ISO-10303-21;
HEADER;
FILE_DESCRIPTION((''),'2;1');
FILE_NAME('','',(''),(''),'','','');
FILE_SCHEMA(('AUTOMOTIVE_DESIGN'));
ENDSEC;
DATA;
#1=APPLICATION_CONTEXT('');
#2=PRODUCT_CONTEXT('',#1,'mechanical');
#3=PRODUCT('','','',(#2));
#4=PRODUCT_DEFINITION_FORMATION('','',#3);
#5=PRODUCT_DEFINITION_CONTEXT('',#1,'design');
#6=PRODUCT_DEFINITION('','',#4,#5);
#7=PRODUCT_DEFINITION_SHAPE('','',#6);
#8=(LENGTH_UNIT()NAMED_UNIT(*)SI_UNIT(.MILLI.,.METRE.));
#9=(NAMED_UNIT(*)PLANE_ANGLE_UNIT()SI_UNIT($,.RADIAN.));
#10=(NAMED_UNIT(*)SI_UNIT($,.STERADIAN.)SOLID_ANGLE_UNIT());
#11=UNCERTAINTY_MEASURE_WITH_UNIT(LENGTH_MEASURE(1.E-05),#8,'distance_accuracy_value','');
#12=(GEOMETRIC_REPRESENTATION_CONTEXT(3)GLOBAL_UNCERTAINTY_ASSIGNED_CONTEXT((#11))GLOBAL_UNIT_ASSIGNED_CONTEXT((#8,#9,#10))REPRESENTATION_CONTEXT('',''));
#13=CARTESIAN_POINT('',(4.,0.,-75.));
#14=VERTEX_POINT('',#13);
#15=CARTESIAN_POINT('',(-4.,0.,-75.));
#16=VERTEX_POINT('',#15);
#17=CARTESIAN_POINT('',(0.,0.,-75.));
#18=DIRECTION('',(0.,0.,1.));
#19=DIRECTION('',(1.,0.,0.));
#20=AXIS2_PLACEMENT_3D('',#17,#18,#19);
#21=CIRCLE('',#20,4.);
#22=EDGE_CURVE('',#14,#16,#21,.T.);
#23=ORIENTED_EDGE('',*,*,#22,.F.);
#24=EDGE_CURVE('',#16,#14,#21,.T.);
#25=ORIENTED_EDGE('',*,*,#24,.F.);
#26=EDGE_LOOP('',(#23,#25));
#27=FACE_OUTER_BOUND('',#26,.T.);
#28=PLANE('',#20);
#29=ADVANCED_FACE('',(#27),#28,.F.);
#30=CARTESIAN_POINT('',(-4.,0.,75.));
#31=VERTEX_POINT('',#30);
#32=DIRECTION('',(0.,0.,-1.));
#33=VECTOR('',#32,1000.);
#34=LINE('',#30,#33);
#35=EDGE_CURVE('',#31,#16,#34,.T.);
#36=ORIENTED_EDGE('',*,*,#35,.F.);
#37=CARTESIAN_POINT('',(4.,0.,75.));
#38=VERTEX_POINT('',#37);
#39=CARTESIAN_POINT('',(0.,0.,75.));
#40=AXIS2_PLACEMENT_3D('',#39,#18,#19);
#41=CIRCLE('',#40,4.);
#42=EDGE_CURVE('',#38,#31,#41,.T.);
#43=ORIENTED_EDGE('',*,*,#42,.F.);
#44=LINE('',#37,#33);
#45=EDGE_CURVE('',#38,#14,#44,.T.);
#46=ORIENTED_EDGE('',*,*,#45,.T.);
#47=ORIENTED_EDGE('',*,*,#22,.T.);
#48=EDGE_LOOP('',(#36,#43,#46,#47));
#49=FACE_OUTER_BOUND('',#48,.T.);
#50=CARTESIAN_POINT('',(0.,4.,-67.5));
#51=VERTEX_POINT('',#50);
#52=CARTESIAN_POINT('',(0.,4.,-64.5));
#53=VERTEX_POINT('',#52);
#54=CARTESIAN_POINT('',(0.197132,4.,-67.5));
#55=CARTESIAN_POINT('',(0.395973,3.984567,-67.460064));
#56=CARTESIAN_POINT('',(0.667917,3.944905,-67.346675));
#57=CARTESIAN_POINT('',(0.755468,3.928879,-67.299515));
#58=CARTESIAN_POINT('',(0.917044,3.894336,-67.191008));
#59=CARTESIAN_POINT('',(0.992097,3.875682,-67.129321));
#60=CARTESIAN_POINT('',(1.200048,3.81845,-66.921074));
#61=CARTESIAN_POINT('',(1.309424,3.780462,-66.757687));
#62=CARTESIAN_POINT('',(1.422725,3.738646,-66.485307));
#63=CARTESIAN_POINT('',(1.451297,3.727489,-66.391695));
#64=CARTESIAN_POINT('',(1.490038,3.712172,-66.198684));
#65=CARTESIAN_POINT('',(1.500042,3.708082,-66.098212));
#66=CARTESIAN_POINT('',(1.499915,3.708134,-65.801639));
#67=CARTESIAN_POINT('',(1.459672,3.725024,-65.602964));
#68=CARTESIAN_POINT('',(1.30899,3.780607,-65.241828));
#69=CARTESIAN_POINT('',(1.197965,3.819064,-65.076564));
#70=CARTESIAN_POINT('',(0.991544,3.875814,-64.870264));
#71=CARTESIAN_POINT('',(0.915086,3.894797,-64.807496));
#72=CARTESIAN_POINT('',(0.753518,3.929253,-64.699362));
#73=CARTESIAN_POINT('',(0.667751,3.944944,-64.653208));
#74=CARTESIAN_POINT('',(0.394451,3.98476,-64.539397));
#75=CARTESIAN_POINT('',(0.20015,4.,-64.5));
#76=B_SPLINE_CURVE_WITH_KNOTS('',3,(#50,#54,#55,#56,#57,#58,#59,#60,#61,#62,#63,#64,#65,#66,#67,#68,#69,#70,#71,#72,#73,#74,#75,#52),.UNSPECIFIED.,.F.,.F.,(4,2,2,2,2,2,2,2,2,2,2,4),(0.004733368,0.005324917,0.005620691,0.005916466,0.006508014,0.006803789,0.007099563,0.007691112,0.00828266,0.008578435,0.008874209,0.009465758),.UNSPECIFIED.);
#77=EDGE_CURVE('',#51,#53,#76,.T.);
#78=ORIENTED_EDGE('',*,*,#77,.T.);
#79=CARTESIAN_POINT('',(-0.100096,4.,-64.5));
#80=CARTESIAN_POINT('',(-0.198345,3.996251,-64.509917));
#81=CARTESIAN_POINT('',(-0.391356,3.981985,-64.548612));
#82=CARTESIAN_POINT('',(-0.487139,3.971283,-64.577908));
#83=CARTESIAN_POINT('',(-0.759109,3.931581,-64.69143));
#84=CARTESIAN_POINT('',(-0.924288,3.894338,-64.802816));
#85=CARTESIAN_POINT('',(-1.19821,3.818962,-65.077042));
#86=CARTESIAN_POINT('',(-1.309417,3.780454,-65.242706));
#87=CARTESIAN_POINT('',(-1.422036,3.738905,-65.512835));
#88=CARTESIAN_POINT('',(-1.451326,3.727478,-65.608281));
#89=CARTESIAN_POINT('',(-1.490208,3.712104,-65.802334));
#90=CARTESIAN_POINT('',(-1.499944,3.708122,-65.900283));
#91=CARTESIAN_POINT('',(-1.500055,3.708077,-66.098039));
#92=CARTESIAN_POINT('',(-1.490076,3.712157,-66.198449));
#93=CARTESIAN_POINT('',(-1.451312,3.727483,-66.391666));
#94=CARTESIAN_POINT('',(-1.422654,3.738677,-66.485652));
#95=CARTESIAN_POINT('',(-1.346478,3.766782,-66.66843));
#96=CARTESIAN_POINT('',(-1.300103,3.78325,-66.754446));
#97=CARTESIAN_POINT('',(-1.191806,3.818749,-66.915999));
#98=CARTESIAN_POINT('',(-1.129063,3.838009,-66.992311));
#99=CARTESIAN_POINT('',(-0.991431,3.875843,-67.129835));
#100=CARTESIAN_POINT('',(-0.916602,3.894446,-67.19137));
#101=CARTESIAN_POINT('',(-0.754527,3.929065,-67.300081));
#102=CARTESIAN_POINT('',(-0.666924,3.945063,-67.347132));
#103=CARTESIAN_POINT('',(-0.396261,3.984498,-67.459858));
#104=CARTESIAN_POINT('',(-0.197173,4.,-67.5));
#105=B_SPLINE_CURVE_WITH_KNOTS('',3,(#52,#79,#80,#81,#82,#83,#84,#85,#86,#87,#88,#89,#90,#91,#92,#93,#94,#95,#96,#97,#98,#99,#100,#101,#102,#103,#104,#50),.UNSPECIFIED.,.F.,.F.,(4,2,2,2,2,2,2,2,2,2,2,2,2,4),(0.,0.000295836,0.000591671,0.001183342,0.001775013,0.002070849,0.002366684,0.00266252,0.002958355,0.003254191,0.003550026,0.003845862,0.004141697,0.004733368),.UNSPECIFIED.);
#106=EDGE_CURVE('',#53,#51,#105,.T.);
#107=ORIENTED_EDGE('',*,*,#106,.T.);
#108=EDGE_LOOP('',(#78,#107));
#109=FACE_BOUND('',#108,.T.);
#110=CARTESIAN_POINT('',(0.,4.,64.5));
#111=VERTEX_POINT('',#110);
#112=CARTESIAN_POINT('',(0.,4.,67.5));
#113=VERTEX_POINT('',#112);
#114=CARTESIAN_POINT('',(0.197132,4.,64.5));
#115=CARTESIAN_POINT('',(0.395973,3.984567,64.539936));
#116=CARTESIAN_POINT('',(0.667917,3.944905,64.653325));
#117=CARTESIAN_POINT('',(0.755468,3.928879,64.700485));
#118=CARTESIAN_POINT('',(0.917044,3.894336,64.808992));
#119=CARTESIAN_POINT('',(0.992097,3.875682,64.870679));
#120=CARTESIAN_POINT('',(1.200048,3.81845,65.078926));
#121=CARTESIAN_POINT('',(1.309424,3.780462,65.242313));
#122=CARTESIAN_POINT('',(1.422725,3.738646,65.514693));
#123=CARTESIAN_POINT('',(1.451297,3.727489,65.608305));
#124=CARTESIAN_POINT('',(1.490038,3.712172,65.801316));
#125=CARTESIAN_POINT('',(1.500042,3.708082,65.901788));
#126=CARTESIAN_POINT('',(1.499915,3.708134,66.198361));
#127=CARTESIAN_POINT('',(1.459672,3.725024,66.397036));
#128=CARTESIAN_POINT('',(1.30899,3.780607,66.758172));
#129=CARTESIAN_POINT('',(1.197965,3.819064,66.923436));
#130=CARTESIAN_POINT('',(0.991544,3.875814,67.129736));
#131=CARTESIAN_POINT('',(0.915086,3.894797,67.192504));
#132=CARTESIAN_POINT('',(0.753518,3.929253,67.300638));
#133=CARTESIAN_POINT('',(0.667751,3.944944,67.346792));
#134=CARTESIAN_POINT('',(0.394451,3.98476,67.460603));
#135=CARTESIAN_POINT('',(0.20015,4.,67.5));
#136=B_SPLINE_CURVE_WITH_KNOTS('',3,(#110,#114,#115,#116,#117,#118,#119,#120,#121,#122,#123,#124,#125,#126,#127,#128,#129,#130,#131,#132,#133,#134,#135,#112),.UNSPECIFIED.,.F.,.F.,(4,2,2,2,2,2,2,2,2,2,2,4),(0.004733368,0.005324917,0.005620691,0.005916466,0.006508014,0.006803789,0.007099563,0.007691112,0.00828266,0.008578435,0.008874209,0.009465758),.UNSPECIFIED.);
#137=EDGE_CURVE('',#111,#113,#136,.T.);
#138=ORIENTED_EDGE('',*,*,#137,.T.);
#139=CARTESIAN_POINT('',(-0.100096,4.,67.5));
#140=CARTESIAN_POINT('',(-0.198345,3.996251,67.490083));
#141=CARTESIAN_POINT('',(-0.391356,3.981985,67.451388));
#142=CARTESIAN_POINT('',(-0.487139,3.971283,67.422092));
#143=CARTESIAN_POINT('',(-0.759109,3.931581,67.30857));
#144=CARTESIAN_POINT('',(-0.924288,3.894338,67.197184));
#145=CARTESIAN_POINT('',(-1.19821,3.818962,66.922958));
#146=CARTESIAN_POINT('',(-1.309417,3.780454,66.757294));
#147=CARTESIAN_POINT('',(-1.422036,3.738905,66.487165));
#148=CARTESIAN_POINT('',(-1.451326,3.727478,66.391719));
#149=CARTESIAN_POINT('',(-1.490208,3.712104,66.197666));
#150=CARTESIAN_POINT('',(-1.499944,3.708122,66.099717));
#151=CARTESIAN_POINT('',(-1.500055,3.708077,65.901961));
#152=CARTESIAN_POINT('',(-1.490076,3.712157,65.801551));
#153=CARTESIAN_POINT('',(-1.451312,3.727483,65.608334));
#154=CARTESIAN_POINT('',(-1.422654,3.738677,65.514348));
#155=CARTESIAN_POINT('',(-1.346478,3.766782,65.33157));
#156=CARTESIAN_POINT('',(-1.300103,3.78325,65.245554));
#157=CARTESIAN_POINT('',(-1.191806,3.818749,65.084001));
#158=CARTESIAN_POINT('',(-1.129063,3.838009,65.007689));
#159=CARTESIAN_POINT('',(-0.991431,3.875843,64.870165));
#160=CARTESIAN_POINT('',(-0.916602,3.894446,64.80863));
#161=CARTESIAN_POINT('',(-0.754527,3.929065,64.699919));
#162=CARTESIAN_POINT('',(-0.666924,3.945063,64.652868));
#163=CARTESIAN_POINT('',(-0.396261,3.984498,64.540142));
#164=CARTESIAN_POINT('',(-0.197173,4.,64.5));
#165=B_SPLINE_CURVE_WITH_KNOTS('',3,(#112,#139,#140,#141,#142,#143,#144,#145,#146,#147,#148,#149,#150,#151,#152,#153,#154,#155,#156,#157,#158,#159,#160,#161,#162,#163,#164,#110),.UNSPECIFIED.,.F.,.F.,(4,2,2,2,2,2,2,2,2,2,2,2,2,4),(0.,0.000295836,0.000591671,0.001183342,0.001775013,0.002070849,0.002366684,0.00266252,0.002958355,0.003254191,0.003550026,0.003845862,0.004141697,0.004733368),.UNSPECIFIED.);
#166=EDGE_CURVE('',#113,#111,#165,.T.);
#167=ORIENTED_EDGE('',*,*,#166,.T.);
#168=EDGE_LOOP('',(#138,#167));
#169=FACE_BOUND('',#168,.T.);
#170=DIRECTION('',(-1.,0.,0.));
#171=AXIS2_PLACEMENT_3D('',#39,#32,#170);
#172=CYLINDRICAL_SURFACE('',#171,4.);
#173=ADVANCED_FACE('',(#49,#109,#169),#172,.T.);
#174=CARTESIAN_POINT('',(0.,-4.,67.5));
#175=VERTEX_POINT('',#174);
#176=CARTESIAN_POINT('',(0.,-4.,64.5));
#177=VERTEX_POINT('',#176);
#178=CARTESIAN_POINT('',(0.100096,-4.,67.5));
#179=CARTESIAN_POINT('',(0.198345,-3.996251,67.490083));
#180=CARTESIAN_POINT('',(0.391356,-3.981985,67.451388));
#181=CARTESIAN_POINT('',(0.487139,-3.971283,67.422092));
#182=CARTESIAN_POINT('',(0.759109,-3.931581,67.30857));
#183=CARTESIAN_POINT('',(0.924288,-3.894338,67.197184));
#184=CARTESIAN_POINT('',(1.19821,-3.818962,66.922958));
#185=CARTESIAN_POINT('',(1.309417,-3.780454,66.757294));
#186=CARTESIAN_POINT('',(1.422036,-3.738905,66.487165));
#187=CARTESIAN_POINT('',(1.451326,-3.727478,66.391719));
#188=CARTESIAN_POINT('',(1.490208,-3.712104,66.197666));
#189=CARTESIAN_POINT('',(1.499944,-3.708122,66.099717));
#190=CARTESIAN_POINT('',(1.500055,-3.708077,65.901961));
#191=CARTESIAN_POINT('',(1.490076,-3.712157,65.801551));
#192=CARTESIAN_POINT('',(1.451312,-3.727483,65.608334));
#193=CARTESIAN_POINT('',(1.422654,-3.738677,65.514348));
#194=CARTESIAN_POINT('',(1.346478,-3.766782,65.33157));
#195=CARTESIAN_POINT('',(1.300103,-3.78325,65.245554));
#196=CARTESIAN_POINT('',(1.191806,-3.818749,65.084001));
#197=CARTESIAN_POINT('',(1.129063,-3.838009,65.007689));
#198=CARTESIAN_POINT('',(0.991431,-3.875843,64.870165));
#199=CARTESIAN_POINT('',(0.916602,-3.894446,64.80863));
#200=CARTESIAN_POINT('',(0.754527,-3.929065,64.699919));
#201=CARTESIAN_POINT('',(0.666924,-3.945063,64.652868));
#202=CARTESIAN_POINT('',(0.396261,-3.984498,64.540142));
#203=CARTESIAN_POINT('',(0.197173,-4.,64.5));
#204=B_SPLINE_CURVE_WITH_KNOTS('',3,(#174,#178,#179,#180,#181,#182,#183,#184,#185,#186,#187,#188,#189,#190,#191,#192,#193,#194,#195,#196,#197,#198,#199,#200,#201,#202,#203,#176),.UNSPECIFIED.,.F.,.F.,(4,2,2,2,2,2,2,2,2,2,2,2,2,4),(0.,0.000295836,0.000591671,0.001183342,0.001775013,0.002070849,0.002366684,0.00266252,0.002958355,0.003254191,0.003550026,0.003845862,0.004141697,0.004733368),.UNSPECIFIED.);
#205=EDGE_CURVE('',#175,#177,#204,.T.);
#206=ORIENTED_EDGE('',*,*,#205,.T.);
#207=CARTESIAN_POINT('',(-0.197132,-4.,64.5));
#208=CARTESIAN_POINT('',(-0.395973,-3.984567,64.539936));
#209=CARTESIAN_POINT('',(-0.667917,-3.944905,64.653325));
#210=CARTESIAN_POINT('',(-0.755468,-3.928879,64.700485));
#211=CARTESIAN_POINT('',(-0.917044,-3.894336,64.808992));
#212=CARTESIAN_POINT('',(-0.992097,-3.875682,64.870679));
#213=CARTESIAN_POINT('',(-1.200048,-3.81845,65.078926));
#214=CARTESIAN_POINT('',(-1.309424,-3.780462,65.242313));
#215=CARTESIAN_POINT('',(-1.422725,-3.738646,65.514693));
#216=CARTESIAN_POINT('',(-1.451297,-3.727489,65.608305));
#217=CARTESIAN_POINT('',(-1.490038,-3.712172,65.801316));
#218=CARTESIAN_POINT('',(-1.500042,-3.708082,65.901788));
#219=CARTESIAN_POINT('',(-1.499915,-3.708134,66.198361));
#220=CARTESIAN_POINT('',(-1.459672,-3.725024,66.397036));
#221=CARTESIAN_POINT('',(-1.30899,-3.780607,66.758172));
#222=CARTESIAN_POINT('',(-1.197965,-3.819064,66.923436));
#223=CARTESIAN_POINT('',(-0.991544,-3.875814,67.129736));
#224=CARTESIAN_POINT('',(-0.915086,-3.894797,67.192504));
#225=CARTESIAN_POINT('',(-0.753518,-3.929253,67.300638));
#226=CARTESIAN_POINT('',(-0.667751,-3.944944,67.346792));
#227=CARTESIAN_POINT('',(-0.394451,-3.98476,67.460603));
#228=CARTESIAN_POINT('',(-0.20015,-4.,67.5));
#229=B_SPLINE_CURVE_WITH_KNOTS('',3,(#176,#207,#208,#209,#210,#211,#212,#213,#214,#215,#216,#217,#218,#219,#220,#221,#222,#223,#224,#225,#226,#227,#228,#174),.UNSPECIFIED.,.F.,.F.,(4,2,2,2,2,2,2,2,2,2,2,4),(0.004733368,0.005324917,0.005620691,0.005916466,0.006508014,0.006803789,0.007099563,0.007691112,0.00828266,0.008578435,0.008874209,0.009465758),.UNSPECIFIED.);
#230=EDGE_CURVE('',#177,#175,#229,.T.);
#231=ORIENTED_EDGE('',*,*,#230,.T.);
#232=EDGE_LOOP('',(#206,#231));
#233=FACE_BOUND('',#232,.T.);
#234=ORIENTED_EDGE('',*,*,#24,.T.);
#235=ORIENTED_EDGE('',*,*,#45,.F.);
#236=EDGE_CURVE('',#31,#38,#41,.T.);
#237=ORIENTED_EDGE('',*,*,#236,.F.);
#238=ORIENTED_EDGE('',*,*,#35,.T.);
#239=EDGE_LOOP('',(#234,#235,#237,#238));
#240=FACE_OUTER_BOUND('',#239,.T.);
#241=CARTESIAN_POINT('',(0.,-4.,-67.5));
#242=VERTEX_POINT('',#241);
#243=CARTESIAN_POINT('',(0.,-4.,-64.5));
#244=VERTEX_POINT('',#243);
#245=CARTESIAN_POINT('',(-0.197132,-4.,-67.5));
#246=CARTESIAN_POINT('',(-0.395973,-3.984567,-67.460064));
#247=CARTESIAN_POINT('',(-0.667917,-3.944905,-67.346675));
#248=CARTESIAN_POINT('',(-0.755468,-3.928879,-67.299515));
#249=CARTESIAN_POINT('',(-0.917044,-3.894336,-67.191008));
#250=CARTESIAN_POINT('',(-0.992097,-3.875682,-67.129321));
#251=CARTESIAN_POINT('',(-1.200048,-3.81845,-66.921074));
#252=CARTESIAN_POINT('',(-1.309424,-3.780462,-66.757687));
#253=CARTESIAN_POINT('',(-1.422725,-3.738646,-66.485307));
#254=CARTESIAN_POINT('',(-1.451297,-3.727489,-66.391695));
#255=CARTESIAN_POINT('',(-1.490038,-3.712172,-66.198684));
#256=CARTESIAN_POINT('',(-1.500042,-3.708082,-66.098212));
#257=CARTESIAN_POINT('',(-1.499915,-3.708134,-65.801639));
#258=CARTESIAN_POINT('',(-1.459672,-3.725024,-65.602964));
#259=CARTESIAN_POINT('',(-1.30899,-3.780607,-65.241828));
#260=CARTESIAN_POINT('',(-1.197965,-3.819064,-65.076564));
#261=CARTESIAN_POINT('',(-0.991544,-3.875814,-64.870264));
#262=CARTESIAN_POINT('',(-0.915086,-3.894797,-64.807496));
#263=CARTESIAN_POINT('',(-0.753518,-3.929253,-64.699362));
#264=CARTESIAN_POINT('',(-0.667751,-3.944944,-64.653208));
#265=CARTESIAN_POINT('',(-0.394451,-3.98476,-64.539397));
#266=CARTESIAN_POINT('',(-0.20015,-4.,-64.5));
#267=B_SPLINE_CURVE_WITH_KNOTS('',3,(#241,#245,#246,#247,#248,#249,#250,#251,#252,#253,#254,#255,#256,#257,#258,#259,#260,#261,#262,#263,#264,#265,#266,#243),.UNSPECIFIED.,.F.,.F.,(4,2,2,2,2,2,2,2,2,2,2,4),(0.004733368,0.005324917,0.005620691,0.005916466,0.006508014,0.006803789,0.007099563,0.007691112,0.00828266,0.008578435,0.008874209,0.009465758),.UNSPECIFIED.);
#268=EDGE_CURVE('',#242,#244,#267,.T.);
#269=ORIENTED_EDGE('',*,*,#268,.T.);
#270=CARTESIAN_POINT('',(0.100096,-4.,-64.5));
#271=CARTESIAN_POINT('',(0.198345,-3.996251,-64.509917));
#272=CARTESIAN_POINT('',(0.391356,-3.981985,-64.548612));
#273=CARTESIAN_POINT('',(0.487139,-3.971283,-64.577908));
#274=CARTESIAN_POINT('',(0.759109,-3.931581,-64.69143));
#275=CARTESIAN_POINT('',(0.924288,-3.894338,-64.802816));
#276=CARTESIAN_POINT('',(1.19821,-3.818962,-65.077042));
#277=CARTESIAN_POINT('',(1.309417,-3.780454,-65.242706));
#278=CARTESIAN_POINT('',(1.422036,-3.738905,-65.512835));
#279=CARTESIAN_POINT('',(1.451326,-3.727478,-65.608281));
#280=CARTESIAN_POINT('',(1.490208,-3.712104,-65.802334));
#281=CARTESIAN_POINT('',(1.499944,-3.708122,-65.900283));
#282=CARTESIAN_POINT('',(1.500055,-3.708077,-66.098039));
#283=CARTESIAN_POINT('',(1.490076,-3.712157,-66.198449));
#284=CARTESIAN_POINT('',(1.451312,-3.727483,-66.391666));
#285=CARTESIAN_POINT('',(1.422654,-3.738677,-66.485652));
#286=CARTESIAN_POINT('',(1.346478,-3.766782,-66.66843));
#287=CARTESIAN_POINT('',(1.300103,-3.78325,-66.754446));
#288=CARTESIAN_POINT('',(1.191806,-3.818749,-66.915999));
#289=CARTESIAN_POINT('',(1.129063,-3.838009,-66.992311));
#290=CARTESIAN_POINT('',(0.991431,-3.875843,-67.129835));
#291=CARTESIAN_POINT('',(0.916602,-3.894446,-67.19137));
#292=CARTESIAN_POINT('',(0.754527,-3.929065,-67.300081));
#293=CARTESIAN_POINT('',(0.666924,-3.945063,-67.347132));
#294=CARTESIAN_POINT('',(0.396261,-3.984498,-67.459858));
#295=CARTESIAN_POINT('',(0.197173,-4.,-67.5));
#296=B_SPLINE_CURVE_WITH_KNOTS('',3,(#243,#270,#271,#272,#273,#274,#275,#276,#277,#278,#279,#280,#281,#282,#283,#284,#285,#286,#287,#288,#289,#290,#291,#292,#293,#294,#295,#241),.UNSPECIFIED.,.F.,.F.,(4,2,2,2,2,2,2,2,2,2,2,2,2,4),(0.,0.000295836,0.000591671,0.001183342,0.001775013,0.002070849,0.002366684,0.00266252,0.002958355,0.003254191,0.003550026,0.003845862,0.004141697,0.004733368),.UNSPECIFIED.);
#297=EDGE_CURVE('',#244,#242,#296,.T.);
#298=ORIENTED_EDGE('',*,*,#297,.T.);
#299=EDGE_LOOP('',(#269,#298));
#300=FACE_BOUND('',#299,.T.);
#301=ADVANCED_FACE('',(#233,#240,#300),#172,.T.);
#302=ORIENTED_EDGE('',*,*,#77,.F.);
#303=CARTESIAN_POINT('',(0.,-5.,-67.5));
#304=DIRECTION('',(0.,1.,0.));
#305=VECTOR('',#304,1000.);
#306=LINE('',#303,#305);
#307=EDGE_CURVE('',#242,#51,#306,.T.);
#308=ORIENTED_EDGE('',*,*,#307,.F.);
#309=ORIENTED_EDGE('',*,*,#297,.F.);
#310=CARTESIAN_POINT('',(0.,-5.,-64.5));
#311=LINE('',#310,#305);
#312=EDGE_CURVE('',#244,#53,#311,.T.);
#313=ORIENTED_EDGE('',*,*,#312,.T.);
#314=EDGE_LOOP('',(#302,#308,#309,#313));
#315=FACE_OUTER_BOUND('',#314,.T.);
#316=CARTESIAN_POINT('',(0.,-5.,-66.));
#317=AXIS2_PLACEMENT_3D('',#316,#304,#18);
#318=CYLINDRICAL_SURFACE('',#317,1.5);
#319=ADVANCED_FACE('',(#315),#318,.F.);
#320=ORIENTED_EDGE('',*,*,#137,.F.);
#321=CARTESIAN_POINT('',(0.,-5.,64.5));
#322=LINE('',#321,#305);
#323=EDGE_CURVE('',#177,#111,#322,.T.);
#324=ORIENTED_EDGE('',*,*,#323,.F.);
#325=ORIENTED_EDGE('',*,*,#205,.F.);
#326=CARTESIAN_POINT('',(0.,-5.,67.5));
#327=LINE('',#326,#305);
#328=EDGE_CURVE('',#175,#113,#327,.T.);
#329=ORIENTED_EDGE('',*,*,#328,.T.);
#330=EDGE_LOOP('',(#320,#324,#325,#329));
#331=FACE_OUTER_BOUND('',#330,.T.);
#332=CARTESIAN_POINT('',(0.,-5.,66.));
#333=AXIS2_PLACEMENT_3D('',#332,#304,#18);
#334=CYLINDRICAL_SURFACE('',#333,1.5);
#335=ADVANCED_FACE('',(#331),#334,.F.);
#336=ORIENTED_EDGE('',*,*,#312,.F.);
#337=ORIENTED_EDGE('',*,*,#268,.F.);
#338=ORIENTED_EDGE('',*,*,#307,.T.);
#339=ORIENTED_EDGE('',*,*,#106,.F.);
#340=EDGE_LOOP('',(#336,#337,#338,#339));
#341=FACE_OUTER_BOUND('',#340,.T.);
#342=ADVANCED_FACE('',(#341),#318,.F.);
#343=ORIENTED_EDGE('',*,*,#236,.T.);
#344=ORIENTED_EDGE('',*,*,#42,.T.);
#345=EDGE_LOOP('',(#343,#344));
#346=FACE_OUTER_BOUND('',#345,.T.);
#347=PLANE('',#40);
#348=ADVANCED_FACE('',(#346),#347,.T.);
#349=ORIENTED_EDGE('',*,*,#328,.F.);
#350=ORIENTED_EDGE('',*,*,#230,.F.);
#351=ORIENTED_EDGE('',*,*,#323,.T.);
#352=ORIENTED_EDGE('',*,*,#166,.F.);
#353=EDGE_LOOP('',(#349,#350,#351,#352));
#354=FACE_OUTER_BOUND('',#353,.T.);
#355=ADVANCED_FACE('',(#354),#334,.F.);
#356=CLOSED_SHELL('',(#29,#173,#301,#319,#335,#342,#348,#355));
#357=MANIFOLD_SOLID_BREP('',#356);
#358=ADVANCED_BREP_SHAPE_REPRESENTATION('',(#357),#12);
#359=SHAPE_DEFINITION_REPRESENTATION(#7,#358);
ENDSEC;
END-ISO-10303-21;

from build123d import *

# Parameters (mm, degrees)
SKETCH1_R           = 4
BOSS_EXTRUDE1_DEPTH = 75
SKETCH3_R           = 1.5
CUT_EXTRUDE1_DEPTH  = 5


with BuildPart() as part:
    # Sketch1 → Boss-Extrude1 (new, symmetric)
    with BuildSketch(Plane.XY):
        Circle(SKETCH1_R)
    extrude(amount=BOSS_EXTRUDE1_DEPTH, both=True)

    # Sketch3 → Cut-Extrude1 (cut, symmetric)
    with BuildSketch(Plane(origin=(0, 0, 0), x_dir=(1, 0, 0), z_dir=(0, 1, 0))):
        with Locations(Location((0, 66, 0), (0, 0, 270))):
            Circle(SKETCH3_R)
        with Locations(Location((0, -66, 0), (0, 0, 270))):
            Circle(SKETCH3_R)
    extrude(amount=CUT_EXTRUDE1_DEPTH, both=True, mode=Mode.SUBTRACT)


solid = part.part
